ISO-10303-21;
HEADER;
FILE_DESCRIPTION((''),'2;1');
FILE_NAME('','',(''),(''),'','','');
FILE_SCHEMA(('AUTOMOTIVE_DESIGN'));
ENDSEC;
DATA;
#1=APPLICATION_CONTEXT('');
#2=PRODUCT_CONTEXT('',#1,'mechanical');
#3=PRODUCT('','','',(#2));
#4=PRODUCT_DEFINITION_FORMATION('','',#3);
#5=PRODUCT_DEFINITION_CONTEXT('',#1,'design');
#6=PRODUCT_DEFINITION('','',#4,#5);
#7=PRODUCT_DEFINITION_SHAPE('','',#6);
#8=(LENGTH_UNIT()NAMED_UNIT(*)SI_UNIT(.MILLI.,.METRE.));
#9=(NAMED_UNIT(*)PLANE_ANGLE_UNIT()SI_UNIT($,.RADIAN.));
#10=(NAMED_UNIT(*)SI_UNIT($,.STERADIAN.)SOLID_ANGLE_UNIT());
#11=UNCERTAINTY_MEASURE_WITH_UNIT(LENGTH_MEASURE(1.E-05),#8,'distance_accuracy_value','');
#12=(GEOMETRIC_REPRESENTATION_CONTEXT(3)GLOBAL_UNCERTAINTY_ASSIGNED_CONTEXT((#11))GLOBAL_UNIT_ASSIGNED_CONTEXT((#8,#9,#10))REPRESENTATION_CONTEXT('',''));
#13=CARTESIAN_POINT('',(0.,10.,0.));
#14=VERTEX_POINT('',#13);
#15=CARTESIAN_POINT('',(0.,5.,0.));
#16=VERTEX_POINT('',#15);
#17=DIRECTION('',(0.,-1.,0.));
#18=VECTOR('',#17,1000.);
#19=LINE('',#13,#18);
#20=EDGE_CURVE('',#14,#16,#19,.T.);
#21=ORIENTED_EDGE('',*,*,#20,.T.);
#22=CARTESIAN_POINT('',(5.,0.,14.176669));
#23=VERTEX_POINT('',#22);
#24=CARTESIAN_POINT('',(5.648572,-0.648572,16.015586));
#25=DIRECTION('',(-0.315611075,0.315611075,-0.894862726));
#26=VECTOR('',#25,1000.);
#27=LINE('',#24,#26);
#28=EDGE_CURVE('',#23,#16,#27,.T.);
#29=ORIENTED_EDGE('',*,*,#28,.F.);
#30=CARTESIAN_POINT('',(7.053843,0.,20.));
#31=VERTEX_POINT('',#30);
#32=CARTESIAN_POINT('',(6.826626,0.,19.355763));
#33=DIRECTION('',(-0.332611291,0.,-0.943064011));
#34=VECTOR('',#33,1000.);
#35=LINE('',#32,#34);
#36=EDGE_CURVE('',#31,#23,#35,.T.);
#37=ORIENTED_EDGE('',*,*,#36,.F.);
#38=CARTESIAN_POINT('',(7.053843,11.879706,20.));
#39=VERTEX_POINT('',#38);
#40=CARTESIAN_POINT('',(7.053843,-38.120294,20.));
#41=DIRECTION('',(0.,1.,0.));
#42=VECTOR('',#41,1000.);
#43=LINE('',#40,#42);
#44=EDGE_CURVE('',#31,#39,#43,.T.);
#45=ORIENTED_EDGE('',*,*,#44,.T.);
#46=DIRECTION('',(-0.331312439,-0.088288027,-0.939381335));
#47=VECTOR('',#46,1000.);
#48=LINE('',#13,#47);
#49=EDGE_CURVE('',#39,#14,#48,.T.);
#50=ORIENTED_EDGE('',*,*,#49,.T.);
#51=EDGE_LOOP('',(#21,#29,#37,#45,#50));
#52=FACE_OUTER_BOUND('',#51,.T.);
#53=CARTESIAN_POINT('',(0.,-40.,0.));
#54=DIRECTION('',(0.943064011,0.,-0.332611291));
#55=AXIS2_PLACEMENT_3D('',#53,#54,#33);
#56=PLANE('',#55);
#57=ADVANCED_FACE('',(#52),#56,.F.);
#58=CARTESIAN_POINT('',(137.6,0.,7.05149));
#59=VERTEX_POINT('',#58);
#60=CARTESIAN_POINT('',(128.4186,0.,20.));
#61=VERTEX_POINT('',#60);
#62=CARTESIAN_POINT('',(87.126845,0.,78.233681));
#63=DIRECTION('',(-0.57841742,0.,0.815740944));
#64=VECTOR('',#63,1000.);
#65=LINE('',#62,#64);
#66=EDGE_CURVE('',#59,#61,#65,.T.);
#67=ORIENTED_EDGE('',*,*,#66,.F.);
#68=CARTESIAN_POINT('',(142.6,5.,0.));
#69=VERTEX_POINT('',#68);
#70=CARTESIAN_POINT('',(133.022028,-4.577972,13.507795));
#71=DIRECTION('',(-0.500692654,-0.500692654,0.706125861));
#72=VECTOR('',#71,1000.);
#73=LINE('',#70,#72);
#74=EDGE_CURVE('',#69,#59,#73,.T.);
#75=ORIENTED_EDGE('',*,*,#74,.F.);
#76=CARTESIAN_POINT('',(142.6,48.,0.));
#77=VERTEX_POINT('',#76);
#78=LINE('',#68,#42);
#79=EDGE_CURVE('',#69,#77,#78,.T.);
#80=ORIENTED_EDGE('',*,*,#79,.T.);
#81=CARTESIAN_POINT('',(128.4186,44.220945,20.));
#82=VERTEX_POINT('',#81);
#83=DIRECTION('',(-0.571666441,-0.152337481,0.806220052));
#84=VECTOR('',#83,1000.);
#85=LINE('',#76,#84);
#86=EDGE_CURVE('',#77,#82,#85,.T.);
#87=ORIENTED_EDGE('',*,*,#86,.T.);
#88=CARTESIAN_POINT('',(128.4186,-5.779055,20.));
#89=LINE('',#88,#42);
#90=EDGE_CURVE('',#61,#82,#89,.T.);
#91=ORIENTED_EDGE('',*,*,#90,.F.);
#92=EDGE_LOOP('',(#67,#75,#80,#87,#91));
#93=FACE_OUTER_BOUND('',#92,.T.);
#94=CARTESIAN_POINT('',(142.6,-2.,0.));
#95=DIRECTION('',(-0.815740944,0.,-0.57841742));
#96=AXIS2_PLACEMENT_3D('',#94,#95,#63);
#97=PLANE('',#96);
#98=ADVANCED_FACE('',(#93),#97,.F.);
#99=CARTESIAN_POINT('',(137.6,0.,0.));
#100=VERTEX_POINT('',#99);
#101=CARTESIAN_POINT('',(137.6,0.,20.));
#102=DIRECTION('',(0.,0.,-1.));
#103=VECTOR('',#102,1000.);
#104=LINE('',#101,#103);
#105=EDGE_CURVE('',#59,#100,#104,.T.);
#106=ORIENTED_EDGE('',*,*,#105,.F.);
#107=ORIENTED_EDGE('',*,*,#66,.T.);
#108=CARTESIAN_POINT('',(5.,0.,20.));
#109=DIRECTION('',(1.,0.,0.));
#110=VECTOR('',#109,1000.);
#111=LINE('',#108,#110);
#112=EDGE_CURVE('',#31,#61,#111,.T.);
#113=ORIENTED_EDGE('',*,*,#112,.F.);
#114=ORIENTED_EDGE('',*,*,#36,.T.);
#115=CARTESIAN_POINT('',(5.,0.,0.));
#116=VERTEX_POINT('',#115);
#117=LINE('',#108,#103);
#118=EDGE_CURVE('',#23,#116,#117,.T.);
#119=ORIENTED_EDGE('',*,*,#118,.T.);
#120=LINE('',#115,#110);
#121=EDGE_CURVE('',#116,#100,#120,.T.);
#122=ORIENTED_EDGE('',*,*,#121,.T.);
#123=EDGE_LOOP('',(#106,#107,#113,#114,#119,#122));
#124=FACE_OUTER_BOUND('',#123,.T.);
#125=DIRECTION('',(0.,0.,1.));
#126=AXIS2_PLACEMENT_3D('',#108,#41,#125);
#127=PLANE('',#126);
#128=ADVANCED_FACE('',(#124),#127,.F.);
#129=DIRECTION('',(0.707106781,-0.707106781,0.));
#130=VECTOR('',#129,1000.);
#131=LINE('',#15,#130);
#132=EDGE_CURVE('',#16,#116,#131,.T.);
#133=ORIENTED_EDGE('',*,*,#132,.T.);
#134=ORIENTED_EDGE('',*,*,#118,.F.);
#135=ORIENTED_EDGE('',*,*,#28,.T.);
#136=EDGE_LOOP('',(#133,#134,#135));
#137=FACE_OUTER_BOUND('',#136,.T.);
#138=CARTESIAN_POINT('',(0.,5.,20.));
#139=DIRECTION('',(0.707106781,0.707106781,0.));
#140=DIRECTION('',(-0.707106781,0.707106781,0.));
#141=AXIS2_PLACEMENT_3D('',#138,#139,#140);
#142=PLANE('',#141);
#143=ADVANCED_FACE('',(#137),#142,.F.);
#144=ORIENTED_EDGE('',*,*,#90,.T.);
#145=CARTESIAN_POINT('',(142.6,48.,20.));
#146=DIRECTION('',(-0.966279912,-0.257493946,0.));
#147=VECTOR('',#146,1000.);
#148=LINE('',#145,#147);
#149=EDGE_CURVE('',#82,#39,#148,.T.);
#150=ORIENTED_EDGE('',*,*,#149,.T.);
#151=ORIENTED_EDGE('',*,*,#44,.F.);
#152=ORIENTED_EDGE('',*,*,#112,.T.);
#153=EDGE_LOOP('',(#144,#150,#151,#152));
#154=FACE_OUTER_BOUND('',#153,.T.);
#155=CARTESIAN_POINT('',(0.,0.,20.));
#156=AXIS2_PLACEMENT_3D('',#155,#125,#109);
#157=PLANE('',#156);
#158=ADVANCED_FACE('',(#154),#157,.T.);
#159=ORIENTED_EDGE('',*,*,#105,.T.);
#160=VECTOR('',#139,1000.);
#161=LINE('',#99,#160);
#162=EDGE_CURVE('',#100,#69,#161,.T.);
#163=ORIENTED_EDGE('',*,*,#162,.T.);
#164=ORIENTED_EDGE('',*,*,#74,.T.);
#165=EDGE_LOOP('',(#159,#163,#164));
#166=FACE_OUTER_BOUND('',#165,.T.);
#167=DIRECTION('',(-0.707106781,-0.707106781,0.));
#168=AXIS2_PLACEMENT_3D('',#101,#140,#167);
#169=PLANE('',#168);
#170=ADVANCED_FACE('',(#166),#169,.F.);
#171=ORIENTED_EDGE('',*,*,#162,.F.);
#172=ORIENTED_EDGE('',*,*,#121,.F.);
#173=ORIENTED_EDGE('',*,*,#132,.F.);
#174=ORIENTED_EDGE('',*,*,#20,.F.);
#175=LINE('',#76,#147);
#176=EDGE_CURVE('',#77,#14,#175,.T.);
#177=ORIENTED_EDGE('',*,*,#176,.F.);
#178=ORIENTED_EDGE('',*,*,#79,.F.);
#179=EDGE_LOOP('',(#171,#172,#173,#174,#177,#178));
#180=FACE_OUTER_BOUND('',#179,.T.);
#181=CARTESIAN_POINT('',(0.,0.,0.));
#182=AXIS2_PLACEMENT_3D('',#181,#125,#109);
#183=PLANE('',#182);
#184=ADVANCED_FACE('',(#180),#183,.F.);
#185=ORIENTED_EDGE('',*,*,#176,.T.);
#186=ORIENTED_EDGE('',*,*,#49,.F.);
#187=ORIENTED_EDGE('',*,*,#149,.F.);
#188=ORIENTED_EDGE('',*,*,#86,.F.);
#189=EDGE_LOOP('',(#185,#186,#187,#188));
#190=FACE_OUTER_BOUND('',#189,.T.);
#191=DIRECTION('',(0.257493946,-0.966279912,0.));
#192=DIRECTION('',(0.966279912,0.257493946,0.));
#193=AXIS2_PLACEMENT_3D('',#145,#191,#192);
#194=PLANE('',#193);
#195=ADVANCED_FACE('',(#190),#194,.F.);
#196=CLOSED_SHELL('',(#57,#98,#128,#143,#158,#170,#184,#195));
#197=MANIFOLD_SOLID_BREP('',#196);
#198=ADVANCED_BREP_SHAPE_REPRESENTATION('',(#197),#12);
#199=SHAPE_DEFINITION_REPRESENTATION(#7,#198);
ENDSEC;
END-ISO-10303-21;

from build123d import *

# Parameters (mm, degrees)
BOSS_EXTRUDE1_DEPTH = 20
CUT_EXTRUDE1_DEPTH  = 50


with BuildPart() as part:
    # Sketch1 → Boss-Extrude1 (new body)
    with BuildSketch(Plane.XY):
        Polygon((5, 0), (137.6, 0), (142.6, 5), (142.6, 48), (0, 10), (0, 5), align=None)
    extrude(amount=BOSS_EXTRUDE1_DEPTH)

    # Sketch2 → Cut-Extrude1 (cut, along a direction that is not the sketch's normal)
    with BuildSketch(Plane(origin=(-2.488112271, 9.33696868, 0), x_dir=(0.9662799118048497, 0.25749394564224604, 0), z_dir=(-0.257493945642246, 0.9662799118048496, 0))):
        Polygon((150.151224814, 0), (135.474939456, -20), (150.151224814, -20), align=None)
        Polygon((2.574939456, -20), (2.574939456, 0), (9.874939456, -20), align=None)
    extrude(amount=-CUT_EXTRUDE1_DEPTH, dir=(0, 1, 0), mode=Mode.SUBTRACT)


solid = part.part
